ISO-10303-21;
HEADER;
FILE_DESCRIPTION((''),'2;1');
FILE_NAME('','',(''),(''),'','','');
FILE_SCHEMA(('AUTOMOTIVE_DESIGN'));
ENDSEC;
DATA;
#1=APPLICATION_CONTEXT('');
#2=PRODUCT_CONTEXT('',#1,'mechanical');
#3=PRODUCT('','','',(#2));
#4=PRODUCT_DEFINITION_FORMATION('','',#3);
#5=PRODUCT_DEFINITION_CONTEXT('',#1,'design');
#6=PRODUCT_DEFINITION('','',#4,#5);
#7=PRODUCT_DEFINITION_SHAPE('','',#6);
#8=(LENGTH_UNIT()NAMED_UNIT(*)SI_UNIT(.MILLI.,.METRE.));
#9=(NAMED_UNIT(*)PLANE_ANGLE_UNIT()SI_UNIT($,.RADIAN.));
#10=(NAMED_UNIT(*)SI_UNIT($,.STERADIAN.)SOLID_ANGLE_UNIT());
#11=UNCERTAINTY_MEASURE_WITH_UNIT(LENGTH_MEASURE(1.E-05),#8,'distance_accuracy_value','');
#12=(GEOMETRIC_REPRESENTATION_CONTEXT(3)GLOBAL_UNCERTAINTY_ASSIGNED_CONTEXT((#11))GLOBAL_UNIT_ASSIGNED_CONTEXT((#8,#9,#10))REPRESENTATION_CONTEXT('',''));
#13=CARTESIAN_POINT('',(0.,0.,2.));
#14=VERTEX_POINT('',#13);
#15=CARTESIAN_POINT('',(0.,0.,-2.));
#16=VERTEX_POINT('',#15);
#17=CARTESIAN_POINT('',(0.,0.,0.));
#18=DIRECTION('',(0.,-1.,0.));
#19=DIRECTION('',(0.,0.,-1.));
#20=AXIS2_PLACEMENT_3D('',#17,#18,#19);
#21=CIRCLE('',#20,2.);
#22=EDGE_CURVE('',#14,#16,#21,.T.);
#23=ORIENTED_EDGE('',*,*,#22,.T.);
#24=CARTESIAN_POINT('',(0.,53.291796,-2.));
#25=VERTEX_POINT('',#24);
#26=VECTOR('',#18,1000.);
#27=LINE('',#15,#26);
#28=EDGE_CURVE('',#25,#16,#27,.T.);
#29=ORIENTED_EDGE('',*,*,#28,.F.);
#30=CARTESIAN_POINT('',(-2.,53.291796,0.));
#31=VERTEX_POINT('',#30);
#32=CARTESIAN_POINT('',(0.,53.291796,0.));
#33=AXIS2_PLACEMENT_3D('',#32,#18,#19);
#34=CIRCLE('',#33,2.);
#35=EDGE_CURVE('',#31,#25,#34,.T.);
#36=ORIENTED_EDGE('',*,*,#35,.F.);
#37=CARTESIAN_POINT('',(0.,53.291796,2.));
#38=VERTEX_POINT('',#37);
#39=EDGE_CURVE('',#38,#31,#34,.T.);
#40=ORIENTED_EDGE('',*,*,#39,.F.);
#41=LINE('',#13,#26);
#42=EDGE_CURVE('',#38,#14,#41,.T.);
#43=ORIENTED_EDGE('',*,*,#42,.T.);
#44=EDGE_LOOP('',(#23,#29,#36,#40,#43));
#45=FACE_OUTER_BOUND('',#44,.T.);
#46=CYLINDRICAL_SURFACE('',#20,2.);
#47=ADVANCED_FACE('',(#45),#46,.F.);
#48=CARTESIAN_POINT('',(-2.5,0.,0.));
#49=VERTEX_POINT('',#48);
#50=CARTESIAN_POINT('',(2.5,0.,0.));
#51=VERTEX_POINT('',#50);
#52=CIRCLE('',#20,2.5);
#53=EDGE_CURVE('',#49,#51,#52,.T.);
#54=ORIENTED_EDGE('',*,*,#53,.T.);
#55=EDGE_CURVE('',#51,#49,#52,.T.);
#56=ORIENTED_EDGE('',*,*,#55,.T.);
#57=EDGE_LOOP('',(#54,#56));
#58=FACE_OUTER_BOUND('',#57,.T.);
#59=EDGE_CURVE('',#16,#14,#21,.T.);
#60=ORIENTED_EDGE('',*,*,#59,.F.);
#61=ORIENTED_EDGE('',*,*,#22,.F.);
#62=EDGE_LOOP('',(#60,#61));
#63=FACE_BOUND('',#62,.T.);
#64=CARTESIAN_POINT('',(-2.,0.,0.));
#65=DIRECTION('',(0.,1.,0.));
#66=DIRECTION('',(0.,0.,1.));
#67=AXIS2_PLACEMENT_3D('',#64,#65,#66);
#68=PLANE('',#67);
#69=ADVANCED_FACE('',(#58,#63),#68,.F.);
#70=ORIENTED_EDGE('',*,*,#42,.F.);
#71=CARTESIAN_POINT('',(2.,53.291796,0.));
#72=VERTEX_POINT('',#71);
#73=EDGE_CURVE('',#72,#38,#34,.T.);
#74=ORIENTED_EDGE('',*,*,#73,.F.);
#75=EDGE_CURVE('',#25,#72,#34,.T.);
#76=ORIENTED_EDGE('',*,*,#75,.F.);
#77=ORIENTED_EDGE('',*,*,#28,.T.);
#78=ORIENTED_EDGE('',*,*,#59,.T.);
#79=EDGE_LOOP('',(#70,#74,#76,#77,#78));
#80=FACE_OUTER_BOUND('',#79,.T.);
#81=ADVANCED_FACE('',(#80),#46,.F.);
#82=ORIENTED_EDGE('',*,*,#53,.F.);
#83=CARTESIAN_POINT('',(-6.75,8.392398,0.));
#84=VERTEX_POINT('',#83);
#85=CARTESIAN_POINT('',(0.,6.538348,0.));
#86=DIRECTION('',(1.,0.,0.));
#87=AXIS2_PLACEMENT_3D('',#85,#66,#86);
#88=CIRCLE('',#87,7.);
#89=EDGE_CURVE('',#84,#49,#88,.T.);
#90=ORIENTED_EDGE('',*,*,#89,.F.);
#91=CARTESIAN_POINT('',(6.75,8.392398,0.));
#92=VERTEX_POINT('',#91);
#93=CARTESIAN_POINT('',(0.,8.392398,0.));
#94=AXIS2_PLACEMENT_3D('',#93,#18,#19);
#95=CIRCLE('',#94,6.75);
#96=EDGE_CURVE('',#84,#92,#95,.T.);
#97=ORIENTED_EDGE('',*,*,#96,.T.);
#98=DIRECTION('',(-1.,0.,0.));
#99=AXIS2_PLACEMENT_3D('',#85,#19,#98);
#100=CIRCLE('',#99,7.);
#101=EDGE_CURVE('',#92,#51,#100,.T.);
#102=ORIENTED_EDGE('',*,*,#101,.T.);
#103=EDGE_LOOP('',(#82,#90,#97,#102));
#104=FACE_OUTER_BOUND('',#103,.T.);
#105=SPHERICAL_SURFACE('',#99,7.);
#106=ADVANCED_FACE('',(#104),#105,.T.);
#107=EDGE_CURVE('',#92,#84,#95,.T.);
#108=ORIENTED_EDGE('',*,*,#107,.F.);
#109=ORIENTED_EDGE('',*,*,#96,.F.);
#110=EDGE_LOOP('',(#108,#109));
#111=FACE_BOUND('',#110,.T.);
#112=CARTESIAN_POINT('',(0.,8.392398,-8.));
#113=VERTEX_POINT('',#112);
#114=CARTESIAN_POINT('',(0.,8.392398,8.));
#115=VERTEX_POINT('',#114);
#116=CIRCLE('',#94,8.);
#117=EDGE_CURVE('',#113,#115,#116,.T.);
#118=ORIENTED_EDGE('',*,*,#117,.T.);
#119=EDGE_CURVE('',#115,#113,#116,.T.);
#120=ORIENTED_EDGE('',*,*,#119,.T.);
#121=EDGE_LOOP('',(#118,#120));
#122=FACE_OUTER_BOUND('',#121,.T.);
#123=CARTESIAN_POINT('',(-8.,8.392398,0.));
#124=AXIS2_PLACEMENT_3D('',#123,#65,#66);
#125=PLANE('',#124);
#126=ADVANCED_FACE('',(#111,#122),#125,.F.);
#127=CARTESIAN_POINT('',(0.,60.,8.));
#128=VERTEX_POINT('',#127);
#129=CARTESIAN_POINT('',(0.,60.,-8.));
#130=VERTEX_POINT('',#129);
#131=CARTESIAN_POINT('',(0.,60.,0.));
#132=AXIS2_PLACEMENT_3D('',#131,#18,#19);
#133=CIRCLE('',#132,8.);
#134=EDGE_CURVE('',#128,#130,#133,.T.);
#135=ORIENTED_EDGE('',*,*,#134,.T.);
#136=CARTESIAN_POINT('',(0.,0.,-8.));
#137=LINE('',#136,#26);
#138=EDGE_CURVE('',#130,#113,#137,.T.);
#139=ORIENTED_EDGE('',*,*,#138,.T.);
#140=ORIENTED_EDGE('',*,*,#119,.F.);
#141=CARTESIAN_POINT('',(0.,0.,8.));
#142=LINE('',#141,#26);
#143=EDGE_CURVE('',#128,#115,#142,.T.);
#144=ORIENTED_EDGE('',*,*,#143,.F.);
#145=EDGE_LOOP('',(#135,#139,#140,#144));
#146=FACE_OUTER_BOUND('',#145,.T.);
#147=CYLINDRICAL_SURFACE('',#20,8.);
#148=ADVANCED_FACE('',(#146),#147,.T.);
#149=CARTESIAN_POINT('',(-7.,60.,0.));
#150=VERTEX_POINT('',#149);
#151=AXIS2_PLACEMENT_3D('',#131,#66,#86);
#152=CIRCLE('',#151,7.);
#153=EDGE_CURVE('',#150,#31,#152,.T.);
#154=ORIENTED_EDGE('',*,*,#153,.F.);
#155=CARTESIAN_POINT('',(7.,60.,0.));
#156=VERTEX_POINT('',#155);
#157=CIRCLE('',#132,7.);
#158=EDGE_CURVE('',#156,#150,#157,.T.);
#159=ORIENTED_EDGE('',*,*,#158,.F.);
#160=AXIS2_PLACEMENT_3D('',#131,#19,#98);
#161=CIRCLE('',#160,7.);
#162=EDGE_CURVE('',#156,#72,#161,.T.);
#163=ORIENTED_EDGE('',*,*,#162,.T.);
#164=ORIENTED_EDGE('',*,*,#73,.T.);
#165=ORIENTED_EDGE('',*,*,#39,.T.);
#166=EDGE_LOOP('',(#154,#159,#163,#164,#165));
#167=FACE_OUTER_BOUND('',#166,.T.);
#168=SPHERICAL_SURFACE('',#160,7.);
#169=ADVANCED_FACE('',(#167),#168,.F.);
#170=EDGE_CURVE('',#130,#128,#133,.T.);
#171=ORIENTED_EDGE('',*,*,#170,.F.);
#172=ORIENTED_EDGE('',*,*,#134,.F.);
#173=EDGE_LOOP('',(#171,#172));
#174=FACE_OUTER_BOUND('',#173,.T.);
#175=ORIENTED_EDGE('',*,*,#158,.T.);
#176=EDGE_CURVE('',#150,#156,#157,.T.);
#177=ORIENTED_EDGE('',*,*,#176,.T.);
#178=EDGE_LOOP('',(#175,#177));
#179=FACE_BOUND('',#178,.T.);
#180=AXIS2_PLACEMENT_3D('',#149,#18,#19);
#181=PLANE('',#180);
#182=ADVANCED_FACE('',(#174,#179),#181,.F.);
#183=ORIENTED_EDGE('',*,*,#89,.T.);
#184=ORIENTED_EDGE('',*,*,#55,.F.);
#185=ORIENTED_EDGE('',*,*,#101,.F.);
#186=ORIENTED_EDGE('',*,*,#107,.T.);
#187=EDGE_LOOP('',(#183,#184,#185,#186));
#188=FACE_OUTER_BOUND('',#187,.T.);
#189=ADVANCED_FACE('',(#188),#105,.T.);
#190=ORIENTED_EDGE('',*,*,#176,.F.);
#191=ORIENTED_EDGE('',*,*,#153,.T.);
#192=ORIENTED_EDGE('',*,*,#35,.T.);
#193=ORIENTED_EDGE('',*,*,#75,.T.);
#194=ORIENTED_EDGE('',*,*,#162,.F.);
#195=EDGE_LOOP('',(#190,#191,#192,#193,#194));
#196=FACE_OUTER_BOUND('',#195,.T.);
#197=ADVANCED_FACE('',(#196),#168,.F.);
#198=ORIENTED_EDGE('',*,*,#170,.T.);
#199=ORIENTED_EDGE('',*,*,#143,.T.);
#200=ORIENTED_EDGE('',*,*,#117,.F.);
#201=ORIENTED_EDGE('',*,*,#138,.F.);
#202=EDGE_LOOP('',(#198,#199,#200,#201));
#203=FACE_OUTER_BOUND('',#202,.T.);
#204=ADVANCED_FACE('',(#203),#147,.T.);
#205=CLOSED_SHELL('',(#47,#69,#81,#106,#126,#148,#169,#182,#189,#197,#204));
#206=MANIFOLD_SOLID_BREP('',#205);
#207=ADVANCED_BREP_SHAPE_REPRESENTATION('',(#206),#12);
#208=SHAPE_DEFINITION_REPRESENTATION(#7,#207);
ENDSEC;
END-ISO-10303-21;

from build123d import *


with BuildPart() as part:
    # Sketch1 → Revolve2 (revolve)
    with BuildSketch(Plane.XY, mode=Mode.PRIVATE) as revolve2_sk:
        with BuildLine():
            Line((-2, 0), (-2, 53.291796068))
            ThreePointArc((-2, 53.291796068), (-5.61248608, 55.816699867), (-7, 60))
            Line((-7, 60), (-8, 60))
            Line((-8, 60), (-8, 8.392398037))
            Line((-8, 8.392398037), (-6.75, 8.392398037))
            ThreePointArc((-6.75, 8.392398037), (-6.244894811, 3.375866985), (-2.5, 0))
            Line((-2.5, 0), (-2, 0))
        make_face()
    revolve(revolve2_sk.sketch.rotate(Axis((0, 0, 0), (0, 1, 0)), 270), axis=Axis((0, 0, 0), (0, 1, 0)))


solid = part.part
